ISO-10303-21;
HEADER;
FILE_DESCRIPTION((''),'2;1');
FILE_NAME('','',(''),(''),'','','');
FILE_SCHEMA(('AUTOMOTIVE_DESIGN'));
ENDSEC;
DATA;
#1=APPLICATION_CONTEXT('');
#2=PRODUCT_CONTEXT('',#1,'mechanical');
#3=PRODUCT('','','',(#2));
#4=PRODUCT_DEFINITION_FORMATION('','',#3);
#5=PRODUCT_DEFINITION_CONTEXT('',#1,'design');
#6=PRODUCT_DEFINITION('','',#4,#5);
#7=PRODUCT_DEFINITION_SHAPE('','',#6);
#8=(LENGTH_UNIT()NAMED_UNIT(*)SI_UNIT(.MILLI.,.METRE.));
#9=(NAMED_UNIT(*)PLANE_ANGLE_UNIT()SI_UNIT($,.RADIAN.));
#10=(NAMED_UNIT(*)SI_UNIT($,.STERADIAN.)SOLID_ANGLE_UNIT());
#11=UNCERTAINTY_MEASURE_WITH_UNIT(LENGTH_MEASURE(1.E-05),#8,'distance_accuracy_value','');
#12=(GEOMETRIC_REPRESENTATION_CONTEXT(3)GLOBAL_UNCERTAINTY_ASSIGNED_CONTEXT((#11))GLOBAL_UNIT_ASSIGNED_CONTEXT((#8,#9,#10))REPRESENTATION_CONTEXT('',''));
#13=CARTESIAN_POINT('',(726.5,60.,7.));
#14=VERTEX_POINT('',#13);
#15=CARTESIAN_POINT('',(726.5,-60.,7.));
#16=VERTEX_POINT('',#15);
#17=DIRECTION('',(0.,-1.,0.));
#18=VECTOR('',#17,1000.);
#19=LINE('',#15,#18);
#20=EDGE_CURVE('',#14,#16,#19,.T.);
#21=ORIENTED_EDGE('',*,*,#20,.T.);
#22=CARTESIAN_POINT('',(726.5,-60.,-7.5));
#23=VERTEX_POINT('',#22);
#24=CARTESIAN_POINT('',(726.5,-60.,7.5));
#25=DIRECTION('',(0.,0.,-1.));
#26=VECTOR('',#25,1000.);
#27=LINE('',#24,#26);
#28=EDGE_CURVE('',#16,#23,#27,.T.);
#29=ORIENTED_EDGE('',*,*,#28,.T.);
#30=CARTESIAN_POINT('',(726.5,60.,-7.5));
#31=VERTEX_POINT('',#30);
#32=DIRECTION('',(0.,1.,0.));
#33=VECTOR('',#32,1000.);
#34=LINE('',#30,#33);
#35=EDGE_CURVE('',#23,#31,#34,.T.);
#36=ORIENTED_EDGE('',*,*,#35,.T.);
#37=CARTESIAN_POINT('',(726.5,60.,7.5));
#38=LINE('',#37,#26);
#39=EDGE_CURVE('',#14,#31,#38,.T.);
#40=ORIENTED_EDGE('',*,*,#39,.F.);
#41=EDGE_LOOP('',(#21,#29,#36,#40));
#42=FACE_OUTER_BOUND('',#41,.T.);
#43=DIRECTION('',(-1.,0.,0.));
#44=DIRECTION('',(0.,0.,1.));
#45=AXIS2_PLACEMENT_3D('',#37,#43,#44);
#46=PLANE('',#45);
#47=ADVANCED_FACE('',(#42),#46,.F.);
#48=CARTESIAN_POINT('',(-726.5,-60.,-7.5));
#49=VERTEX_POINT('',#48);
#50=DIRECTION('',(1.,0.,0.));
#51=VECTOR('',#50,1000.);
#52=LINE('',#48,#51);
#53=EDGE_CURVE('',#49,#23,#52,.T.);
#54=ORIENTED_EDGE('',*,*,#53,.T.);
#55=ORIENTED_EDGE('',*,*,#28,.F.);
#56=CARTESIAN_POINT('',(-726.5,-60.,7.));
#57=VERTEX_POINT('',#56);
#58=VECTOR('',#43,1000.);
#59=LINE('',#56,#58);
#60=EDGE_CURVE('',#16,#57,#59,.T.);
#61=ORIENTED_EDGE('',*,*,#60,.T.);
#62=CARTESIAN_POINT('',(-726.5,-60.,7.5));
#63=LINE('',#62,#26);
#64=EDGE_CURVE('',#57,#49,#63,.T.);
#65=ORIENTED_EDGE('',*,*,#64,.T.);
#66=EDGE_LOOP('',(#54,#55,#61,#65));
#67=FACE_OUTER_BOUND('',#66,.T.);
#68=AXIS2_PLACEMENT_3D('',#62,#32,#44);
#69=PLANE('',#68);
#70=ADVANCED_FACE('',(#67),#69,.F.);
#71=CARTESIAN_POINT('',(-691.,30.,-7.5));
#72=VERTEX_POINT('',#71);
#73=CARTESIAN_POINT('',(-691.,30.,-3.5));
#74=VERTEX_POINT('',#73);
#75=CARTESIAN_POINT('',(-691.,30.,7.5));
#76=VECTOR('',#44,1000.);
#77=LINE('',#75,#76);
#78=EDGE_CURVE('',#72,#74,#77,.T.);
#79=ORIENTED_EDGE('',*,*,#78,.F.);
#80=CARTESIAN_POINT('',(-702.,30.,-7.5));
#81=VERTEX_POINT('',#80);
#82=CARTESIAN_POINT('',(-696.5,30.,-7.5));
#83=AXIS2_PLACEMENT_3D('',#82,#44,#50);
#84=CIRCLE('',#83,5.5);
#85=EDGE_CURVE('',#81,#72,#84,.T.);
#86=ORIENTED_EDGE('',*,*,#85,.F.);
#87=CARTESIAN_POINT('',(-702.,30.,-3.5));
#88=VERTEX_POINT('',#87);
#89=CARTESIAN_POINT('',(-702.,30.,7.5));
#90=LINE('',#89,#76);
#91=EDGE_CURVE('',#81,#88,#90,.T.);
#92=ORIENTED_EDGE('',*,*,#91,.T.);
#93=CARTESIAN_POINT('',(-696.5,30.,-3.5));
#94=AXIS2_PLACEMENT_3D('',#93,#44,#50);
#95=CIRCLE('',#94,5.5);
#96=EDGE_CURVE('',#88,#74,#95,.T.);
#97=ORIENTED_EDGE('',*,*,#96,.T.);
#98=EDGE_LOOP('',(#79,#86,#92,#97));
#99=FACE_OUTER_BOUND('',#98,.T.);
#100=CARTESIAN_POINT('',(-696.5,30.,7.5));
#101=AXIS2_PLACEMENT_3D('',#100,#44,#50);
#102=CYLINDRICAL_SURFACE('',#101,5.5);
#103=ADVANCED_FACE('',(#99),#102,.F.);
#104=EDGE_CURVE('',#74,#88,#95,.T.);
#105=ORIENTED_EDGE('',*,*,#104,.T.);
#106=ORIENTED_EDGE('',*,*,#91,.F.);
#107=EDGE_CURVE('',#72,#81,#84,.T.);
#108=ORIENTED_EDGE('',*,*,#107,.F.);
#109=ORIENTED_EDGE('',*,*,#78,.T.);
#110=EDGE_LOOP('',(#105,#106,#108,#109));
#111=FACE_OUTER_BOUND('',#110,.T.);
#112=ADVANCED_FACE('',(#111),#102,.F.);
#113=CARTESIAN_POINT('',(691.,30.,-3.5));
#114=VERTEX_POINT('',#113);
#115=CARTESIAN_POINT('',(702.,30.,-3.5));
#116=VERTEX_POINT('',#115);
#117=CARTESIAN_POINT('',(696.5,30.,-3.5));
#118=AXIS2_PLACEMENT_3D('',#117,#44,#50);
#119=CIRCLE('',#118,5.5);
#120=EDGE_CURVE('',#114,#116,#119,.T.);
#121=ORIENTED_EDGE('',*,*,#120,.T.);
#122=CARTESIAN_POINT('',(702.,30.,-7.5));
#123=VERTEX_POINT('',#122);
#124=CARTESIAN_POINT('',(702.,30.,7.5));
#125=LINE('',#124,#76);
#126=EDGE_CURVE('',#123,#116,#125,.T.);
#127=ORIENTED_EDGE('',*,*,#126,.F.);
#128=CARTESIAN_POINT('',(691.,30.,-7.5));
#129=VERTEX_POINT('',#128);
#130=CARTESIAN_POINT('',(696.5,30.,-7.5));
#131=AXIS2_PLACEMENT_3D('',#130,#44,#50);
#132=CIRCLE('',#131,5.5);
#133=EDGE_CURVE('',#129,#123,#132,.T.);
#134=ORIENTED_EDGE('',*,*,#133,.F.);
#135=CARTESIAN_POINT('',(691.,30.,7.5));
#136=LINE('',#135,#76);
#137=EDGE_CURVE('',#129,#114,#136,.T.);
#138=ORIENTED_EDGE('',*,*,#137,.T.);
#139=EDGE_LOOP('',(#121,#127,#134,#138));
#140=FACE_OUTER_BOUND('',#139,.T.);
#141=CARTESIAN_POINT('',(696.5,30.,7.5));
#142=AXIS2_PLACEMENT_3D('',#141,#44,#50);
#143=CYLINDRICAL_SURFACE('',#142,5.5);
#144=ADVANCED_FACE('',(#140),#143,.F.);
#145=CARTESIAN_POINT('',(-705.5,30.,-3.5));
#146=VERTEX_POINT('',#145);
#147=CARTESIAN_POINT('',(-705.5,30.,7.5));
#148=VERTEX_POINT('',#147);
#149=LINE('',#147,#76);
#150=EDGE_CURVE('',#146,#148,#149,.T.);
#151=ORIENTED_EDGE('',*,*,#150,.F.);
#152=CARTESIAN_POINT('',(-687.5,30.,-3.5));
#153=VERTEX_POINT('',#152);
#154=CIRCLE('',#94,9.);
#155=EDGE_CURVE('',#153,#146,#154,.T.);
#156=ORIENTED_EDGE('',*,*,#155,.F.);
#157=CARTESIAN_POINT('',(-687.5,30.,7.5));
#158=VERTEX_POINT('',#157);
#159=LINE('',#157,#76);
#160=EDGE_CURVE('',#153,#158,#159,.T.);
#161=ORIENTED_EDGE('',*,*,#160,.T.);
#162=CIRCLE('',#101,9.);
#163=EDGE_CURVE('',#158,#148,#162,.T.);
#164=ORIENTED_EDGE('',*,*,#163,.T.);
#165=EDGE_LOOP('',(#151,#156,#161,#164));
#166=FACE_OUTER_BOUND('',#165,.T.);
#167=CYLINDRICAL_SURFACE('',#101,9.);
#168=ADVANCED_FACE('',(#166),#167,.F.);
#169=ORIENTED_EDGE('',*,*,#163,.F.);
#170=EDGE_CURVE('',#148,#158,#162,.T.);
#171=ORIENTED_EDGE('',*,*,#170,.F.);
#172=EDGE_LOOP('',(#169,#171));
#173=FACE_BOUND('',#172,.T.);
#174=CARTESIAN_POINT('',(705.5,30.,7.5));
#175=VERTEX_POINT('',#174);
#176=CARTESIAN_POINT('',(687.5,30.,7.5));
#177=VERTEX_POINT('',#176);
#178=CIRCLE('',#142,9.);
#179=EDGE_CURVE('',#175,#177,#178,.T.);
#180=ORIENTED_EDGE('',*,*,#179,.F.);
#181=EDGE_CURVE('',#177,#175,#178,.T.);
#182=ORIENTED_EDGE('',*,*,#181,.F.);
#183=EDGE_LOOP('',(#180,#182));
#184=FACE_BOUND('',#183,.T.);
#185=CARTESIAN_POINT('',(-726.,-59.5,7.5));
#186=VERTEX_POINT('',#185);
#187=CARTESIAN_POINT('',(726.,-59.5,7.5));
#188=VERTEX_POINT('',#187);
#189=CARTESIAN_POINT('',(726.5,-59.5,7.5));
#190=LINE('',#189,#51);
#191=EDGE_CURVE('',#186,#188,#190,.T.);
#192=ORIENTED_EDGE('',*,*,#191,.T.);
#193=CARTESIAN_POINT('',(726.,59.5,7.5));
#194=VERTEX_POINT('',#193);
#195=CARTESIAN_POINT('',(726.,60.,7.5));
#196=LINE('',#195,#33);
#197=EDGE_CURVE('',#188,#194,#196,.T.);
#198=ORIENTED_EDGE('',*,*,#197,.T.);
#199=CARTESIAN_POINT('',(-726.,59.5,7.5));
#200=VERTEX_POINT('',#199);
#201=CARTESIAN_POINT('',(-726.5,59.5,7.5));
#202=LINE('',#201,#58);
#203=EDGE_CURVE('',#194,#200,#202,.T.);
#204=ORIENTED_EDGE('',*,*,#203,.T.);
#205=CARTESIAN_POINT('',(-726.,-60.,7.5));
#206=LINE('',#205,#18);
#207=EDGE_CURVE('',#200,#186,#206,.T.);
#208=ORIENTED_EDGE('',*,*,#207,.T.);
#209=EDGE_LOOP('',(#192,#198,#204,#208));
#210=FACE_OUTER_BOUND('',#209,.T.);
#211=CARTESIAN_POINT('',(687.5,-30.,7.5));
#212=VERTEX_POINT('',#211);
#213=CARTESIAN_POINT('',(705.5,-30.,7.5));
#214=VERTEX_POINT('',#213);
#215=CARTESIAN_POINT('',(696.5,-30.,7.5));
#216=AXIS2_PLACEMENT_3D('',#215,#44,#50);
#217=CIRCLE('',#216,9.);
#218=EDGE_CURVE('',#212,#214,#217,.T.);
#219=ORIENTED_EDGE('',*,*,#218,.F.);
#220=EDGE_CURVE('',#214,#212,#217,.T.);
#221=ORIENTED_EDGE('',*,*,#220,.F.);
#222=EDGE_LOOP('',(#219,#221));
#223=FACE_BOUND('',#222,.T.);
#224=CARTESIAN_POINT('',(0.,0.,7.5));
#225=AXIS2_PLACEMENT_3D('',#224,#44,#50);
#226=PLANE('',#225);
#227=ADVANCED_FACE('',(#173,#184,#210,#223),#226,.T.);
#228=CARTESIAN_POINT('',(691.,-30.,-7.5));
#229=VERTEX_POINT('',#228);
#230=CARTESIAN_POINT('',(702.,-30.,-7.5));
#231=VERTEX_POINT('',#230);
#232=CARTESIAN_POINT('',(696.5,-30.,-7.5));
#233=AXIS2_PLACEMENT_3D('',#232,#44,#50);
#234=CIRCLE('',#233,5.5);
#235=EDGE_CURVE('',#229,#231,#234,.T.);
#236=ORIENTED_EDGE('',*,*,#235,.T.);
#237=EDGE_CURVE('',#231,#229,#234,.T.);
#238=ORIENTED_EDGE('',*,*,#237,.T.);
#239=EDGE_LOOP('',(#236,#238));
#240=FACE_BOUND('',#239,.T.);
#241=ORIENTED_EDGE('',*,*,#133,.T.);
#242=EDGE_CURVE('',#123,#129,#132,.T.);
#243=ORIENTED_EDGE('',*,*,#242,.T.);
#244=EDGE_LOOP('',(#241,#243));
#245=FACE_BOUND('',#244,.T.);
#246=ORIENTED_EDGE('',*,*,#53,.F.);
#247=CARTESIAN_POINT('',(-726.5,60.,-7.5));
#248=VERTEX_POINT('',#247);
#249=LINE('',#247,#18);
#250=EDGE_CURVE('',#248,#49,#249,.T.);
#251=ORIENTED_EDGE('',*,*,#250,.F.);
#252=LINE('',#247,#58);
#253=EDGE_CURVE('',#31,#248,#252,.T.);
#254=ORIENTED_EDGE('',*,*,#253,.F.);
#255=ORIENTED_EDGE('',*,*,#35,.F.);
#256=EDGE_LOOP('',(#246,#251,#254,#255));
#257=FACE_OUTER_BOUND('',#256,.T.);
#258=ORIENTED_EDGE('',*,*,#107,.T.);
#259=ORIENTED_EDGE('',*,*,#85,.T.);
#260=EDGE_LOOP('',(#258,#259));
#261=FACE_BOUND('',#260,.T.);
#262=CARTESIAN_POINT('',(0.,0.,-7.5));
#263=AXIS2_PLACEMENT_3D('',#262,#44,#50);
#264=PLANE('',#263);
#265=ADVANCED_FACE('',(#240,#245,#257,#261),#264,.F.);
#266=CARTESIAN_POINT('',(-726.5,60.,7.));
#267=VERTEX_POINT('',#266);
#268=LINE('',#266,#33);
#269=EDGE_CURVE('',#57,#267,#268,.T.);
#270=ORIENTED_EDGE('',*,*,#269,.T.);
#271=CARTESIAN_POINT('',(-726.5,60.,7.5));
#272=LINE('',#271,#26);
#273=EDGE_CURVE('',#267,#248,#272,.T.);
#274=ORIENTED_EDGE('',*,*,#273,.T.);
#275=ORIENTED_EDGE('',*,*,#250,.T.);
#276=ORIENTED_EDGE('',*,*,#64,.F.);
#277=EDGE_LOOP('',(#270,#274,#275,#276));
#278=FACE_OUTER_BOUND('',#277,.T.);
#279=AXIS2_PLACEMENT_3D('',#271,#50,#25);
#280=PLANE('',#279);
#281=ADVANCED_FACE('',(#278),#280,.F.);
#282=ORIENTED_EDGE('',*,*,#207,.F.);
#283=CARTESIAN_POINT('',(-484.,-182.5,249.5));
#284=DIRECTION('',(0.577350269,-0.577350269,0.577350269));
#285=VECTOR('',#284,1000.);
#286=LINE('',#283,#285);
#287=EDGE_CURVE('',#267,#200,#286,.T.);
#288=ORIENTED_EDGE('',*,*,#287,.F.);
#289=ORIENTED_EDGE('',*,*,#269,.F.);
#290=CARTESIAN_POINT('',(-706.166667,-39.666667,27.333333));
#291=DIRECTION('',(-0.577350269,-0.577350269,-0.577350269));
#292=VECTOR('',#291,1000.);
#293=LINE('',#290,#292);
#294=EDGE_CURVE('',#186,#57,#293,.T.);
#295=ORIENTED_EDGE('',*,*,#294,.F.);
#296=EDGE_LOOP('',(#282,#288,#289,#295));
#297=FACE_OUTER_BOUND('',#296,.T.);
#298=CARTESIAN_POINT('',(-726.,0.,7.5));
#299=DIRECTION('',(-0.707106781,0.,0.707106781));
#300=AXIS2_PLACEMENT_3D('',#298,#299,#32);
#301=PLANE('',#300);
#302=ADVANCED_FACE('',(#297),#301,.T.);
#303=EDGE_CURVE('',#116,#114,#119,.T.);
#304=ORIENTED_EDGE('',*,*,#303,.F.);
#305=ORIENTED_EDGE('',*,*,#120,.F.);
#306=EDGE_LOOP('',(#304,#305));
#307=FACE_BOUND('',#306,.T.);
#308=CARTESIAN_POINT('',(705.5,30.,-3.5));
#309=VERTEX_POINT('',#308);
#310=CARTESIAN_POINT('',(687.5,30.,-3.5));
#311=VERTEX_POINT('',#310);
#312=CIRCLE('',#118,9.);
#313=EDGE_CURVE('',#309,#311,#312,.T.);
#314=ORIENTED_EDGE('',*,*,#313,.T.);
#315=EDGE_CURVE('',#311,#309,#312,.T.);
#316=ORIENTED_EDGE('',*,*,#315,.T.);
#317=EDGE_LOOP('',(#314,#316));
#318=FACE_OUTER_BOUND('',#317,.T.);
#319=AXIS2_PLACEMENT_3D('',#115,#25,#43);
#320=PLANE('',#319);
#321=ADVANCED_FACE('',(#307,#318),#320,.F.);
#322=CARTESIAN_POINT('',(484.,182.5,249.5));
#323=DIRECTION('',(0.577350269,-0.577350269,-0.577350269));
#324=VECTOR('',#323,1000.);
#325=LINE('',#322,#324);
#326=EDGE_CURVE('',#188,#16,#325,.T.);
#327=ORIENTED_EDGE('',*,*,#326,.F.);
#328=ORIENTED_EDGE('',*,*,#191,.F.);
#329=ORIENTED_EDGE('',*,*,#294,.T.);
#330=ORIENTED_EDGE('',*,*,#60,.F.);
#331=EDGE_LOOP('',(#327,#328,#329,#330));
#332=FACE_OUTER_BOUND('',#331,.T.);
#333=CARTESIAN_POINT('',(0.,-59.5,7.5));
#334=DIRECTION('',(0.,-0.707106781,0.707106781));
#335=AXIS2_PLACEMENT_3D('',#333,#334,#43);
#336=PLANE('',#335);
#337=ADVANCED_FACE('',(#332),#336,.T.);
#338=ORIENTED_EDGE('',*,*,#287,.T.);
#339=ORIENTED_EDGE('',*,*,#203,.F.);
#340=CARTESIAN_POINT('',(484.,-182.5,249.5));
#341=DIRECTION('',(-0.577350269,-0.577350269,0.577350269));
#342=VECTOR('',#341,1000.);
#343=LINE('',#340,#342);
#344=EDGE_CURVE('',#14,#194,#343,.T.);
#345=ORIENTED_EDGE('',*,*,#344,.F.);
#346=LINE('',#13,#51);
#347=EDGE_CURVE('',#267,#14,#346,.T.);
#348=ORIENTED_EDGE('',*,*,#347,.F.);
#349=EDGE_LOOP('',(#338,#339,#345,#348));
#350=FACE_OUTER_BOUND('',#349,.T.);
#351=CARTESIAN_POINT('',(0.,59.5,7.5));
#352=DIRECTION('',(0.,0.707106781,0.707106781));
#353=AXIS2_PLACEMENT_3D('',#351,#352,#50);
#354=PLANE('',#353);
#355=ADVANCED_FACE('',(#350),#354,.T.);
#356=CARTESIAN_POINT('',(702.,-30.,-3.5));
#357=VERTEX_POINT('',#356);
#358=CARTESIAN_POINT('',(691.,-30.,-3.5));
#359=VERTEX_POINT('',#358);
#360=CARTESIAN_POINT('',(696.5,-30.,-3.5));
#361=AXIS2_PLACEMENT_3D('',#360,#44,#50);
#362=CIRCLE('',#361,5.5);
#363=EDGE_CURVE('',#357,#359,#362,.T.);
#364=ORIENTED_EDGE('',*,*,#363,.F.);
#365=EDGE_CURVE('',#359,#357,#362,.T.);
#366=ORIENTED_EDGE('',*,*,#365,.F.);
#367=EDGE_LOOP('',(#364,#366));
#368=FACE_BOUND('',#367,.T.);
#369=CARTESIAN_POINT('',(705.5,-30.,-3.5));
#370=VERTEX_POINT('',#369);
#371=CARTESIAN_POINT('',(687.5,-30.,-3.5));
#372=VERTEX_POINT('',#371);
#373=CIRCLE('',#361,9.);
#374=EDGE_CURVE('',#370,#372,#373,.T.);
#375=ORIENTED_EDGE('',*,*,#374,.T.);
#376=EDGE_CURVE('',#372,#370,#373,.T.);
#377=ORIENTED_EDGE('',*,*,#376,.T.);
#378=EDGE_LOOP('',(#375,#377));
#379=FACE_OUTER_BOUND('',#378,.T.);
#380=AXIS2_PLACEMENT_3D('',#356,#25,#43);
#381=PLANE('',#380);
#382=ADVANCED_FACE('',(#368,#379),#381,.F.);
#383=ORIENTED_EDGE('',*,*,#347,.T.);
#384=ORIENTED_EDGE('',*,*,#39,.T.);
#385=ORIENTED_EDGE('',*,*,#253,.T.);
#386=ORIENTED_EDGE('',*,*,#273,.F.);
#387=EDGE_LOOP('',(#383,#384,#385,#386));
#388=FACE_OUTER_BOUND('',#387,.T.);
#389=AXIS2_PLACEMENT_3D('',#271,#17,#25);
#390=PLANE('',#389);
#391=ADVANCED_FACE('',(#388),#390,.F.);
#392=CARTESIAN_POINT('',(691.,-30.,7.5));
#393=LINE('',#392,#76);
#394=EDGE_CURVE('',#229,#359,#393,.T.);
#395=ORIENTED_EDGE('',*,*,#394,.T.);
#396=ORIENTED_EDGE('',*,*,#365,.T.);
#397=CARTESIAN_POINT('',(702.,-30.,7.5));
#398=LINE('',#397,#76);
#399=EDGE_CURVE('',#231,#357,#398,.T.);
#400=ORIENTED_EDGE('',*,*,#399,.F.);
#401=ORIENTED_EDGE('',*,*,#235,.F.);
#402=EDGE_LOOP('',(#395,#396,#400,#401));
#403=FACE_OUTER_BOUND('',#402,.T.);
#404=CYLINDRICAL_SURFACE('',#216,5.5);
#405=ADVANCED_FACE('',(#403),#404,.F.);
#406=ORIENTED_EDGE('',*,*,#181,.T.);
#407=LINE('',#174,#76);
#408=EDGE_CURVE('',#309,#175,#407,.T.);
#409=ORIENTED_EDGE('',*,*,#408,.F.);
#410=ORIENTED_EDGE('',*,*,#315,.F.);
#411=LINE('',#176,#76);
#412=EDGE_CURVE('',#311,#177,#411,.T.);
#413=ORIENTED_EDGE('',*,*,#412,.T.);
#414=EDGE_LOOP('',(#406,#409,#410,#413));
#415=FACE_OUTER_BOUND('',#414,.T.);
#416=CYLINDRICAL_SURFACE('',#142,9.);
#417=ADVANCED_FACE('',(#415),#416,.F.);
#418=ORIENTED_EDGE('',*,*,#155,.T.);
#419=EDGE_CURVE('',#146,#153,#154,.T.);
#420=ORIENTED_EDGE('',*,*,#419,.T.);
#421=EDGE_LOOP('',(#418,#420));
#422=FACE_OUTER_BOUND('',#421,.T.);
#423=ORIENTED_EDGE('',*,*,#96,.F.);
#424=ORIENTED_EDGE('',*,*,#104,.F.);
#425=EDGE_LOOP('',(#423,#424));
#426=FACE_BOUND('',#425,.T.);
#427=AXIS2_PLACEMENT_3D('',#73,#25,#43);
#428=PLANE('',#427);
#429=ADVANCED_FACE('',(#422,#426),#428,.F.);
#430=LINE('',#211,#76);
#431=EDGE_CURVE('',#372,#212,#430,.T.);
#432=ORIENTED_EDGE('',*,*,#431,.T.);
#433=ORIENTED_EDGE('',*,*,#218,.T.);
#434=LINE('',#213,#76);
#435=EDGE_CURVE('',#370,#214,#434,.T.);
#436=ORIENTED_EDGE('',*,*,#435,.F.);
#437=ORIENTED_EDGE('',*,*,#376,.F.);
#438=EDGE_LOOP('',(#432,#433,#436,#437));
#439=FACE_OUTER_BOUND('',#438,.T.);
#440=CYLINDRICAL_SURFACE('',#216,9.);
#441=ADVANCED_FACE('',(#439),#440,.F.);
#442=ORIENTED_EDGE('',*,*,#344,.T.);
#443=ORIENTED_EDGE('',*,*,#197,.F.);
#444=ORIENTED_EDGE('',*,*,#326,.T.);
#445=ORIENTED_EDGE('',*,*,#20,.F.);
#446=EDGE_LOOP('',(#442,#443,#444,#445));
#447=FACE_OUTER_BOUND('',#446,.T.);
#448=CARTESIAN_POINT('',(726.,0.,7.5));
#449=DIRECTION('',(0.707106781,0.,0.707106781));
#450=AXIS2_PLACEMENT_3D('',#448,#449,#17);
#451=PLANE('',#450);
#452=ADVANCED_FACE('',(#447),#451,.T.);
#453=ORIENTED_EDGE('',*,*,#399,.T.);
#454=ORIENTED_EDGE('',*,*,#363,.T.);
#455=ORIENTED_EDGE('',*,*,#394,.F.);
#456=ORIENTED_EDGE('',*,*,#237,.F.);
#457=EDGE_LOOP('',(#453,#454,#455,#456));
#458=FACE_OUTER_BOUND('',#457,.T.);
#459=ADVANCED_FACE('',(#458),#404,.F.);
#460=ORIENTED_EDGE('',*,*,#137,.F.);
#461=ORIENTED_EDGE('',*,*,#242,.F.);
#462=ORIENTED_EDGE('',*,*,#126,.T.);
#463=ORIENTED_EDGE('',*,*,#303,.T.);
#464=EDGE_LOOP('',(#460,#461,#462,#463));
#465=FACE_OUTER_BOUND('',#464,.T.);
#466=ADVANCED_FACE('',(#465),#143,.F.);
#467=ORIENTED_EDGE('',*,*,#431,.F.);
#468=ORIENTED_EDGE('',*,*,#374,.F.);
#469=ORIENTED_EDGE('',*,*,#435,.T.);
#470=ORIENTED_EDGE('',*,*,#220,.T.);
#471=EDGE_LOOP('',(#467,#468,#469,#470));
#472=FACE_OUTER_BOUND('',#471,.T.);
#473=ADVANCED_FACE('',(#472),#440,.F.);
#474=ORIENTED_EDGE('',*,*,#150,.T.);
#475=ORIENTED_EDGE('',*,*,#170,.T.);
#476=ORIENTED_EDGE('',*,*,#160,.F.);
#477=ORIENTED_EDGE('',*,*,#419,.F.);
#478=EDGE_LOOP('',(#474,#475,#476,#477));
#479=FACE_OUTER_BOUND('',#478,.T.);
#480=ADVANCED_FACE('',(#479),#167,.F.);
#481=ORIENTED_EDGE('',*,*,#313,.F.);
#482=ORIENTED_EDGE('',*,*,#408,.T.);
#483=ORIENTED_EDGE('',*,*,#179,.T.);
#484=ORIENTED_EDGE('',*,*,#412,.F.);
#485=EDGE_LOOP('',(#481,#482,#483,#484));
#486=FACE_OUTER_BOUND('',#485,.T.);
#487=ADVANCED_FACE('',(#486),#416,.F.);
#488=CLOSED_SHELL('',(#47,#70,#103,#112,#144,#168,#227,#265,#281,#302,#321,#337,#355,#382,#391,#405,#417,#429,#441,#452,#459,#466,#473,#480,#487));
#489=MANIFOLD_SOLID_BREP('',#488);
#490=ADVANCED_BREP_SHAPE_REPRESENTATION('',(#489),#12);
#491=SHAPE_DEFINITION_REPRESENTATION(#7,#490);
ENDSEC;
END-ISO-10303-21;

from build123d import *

# Parameters (mm, degrees)
SKETCH_1_W                = 1453
SKETCH_1_H                = 120
EXTRUDE_1_DEPTH           = 7.5
HOLE_WIZARD_1_D           = 11
HOLE_WIZARD_1_CBORE_D     = 18
HOLE_WIZARD_1_CBORE_DEPTH = 11
HOLE_WIZARD_2_D           = 11
HOLE_WIZARD_2_CBORE_D     = 18
HOLE_WIZARD_2_CBORE_DEPTH = 11
CHAMFER_1_SIZE            = 0.5


with BuildPart() as part:
    # 草图1 → 凸台-拉伸1 (new, symmetric)
    with BuildSketch(Plane.XY):
        Rectangle(SKETCH_1_W, SKETCH_1_H)
    extrude(amount=EXTRUDE_1_DEPTH, both=True)

    # 打孔尺寸(%根据)内六角圆柱头螺钉的类型1 (through all)
    with Locations(Plane(origin=(-696.5, 30, 7.5), x_dir=(1, 0, 0), z_dir=(0, 0, 1))):
        with Locations((0, 0)):
            CounterBoreHole(HOLE_WIZARD_1_D / 2, HOLE_WIZARD_1_CBORE_D / 2, HOLE_WIZARD_1_CBORE_DEPTH)

    # 打孔尺寸(%根据)内六角圆柱头螺钉的类型2 (through all)
    with Locations(Plane(origin=(696.5, 30, 7.5), x_dir=(1, 0, 0), z_dir=(0, 0, 1))):
        with Locations((0, 0), (0, -60)):
            CounterBoreHole(HOLE_WIZARD_2_D / 2, HOLE_WIZARD_2_CBORE_D / 2, HOLE_WIZARD_2_CBORE_DEPTH)

    # 倒角1
    chamfer_1_edges = [part.edges().sort_by_distance(p)[0] for p in [
        (-726.5, 0, 7.5),
        (0, -60, 7.5),
        (726.5, 0, 7.5),
        (0, 60, 7.5),
    ]]
    chamfer(chamfer_1_edges, length=CHAMFER_1_SIZE)


solid = part.part
